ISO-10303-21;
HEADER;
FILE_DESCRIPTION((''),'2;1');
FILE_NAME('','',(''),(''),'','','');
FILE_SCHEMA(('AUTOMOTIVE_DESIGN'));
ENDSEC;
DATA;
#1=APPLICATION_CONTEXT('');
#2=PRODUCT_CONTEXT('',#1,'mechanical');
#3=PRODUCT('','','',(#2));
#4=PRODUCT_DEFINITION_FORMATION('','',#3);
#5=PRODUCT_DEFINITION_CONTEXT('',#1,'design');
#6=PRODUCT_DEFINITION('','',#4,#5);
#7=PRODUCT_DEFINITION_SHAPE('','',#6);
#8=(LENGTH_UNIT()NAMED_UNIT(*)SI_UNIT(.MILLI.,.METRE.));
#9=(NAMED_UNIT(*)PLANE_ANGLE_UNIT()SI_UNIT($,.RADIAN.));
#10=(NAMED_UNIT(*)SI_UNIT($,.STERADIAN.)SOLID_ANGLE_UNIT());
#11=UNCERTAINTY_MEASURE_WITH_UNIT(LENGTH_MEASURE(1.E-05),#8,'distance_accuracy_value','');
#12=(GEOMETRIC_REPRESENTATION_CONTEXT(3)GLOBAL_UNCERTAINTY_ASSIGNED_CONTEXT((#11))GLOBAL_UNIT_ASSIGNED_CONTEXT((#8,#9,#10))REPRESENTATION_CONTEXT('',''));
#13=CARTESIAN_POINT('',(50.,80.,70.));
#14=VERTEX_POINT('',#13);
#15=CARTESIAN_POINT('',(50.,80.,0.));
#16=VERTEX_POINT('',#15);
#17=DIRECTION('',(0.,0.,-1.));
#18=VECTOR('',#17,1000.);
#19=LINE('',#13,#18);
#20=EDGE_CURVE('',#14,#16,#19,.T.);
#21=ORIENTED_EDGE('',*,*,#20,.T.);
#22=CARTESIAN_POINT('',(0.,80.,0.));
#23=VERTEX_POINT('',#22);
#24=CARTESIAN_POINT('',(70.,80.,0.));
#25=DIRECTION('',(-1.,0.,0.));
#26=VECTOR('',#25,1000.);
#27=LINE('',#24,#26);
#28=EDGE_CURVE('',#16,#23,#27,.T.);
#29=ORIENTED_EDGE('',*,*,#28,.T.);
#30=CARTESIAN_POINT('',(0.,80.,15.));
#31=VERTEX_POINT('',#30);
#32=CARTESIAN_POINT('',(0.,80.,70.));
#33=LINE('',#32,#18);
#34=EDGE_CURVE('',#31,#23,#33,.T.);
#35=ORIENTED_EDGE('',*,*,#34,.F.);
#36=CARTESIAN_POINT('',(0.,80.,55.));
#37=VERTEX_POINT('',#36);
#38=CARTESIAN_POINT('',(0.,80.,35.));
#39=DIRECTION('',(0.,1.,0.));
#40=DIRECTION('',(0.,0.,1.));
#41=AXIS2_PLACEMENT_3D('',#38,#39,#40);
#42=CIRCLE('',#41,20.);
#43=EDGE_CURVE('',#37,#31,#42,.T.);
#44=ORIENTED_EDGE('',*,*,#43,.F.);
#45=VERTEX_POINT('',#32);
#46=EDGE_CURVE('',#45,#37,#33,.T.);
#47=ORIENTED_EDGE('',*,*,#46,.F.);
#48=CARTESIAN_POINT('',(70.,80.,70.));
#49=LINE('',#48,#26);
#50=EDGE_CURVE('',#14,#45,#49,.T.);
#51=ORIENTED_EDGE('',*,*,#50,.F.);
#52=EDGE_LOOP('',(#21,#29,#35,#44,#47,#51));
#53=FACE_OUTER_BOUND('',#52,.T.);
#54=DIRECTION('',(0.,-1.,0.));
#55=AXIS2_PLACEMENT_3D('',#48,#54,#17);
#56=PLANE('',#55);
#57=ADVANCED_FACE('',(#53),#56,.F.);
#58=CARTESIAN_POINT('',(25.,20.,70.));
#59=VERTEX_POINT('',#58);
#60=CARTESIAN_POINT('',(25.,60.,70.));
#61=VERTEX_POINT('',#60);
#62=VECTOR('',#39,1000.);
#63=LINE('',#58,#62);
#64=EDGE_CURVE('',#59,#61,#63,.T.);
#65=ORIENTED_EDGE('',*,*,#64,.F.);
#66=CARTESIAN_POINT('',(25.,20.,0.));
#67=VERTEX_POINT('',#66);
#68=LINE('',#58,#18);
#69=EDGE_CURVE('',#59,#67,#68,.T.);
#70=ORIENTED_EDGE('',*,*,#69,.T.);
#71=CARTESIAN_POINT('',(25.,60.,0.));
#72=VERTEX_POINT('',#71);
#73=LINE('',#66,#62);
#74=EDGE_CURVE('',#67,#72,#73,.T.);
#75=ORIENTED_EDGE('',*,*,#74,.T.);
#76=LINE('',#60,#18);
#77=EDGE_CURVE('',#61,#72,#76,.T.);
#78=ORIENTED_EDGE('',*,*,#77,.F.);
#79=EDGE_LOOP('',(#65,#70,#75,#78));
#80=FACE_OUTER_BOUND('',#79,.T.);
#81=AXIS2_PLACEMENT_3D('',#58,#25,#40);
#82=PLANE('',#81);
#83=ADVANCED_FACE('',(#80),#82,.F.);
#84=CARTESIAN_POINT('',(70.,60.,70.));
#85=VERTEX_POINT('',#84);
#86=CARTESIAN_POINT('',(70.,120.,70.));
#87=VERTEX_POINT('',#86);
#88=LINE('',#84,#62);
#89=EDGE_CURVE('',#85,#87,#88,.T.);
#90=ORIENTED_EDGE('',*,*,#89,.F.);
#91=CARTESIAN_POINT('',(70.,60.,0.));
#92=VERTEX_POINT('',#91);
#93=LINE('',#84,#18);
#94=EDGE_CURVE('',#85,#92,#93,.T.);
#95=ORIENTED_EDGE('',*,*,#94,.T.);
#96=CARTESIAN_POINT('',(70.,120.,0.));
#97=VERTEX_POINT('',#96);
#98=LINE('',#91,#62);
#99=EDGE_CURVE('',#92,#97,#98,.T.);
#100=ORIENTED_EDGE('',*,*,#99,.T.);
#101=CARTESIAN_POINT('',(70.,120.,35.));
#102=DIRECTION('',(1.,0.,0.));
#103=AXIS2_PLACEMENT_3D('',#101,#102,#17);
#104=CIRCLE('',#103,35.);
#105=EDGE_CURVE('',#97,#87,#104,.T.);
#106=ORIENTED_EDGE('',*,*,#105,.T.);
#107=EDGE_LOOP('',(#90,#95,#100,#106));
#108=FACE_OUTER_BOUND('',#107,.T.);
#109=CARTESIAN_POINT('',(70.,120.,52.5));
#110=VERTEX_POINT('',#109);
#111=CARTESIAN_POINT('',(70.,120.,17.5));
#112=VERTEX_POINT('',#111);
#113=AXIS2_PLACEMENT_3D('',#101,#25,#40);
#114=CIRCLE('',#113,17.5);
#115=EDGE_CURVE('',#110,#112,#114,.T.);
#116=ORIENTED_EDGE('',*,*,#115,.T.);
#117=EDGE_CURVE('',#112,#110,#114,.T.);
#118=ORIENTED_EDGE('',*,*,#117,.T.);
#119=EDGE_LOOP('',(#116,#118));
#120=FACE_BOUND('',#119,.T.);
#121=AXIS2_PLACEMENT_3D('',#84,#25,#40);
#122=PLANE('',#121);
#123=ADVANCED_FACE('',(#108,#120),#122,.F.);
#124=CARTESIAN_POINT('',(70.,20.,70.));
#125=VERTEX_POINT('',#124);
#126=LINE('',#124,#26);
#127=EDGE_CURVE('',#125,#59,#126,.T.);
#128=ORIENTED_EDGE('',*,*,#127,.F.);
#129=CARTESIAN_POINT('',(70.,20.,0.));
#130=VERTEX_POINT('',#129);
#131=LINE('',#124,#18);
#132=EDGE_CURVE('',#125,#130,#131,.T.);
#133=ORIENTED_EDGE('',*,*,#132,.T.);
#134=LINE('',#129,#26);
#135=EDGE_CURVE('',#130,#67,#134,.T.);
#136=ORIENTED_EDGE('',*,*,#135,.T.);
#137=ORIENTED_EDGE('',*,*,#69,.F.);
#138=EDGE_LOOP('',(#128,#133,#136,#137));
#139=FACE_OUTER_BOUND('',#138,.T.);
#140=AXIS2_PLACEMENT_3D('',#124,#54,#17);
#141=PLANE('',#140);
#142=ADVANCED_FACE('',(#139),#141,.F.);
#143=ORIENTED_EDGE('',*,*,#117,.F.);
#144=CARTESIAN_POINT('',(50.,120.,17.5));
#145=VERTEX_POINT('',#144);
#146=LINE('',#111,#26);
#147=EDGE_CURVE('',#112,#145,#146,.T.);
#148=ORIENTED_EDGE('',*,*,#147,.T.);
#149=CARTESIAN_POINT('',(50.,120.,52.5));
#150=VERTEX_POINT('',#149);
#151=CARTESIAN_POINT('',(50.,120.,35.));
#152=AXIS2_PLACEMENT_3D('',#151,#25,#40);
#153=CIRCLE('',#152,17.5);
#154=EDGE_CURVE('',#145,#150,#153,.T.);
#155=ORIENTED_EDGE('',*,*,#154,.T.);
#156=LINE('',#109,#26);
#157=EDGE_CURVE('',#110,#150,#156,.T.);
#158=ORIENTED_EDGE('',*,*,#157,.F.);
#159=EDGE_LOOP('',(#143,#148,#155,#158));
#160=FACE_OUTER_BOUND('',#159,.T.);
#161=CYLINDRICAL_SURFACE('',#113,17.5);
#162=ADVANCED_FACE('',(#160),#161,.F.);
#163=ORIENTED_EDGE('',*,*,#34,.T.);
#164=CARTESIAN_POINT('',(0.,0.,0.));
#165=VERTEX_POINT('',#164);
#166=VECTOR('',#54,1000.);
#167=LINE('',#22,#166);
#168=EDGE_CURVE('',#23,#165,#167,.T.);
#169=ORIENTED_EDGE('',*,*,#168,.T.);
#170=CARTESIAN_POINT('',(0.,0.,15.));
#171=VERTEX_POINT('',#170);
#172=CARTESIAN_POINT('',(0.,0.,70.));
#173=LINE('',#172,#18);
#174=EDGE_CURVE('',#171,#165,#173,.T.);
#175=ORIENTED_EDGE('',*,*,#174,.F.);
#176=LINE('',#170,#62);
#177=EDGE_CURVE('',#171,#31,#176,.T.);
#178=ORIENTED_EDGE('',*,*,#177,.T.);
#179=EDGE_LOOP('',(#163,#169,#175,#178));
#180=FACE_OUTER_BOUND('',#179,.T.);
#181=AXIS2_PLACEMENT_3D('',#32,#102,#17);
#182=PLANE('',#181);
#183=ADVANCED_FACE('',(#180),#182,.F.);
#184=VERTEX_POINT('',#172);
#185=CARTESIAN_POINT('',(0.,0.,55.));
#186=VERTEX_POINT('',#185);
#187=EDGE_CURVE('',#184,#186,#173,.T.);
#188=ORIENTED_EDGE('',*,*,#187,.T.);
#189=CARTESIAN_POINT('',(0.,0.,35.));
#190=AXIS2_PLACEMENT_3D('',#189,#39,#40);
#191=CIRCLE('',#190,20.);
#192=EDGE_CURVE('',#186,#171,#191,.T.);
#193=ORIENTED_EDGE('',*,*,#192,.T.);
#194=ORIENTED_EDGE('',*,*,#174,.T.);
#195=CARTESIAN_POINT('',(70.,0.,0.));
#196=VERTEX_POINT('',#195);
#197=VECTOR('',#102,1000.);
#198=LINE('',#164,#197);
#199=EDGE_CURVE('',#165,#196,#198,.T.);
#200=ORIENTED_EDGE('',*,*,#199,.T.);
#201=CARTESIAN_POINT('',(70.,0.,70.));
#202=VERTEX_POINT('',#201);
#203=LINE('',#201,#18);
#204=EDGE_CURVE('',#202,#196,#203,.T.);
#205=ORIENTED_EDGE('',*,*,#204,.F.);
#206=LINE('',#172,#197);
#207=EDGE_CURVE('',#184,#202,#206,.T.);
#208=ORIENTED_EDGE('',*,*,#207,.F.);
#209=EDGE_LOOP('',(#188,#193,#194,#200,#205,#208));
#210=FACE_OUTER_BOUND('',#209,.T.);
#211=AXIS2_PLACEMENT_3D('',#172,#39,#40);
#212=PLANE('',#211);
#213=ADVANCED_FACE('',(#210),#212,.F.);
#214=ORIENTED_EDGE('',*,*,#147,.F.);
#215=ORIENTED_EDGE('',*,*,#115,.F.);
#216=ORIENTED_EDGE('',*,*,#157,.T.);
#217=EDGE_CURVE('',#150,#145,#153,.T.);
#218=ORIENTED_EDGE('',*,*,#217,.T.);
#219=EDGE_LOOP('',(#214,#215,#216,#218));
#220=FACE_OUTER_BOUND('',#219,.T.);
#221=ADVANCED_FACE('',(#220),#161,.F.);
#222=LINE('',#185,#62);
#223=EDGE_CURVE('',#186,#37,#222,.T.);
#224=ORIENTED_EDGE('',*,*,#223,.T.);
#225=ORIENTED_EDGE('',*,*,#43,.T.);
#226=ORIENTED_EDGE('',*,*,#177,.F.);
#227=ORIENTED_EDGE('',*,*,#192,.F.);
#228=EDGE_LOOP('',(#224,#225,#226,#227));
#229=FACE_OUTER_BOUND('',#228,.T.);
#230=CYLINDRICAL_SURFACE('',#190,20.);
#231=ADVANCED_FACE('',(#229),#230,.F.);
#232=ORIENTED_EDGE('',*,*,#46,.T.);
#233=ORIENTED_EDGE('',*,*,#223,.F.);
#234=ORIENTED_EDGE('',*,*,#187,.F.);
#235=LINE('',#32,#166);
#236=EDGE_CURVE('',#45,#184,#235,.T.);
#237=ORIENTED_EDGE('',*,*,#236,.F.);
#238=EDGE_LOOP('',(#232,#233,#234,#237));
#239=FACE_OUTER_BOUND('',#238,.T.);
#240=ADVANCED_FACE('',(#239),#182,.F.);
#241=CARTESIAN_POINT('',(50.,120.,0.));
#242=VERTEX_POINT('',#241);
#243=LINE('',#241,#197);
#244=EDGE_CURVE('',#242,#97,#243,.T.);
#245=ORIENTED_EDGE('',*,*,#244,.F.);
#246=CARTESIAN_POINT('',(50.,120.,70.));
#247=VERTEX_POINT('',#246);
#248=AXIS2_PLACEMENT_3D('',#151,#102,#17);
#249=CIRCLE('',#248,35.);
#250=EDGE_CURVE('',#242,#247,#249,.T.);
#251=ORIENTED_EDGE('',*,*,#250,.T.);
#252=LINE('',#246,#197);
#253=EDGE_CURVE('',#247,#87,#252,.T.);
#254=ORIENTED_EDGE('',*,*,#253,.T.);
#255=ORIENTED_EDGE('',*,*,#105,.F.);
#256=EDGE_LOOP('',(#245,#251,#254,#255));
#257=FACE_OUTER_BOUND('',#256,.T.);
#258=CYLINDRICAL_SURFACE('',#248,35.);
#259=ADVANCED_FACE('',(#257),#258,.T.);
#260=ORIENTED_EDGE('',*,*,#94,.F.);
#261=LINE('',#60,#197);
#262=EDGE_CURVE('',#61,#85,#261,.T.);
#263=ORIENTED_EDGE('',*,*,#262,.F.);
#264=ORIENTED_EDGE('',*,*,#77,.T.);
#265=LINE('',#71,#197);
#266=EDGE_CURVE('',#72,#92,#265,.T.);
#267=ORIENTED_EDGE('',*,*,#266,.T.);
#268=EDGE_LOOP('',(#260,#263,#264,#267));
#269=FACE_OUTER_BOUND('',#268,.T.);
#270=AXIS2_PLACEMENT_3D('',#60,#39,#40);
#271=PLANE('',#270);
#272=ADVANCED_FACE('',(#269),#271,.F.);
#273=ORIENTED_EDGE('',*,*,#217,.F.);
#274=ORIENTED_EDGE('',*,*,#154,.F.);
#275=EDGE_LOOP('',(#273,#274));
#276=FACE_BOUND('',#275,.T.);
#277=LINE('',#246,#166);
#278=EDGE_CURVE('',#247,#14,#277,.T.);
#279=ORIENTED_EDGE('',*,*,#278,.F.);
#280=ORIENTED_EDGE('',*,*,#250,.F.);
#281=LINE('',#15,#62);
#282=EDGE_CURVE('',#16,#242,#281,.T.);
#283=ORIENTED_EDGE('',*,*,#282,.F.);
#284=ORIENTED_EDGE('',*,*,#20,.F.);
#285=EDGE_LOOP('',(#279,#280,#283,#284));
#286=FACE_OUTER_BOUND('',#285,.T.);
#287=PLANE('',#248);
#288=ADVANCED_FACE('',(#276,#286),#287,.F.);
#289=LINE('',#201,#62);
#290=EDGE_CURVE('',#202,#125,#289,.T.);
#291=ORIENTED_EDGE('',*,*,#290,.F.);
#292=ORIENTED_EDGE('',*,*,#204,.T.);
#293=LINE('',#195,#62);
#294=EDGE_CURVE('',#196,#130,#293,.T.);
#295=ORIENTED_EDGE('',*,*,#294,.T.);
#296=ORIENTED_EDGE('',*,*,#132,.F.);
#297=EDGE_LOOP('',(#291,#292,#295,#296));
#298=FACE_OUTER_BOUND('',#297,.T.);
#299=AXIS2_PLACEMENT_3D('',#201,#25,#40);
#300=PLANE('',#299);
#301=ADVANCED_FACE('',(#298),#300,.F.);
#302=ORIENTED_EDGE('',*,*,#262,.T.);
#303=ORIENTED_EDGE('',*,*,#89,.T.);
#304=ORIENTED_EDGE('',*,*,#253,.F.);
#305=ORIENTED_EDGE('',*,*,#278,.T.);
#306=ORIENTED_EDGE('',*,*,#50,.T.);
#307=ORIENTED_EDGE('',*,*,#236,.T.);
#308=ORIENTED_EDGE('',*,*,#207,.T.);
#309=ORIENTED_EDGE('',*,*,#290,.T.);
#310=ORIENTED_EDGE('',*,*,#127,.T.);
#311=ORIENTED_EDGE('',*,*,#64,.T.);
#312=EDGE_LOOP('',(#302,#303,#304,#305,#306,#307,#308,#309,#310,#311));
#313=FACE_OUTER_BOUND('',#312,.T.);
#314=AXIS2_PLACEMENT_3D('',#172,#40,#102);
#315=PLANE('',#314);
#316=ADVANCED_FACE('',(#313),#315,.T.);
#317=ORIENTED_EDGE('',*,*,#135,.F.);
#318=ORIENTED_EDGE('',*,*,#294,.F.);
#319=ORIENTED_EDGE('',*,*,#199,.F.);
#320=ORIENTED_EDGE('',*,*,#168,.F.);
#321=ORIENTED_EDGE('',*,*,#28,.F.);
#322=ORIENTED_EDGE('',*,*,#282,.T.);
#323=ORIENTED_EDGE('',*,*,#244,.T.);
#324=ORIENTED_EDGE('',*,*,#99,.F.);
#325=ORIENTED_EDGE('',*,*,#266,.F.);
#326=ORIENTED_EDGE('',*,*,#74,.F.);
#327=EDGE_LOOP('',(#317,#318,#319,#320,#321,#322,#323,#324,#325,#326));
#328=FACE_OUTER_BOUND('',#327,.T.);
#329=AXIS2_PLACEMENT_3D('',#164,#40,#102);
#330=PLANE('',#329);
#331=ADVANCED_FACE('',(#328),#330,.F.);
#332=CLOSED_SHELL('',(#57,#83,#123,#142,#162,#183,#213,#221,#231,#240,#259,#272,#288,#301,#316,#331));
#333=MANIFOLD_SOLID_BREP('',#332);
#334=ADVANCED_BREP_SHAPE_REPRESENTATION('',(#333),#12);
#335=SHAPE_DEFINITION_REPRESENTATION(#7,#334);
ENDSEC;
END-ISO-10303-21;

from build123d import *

# Parameters (mm, degrees)
BRACKET_BODY_DEPTH     = 70
ARC_NOTCH_CUT_DEPTH    = 80
LUG_DEPTH              = 20
LUG_HOLE_SKETCH_R      = 17.5
LUG_THROUGH_HOLE_DEPTH = 20


with BuildPart() as part:
    # Bracket Profile Sketch → Bracket Body (new body)
    with BuildSketch(Plane.XY):
        Polygon((0, 0), (70, 0), (70, 20), (25, 20), (25, 60), (70, 60), (70, 80), (0, 80), align=None)
    extrude(amount=BRACKET_BODY_DEPTH)

    # Arc Notch Sketch → Arc Notch Cut (cut)
    with BuildSketch(Plane(origin=(0, 80, 0), x_dir=(1, 0, 0), z_dir=(0, 1, 0))):
        with BuildLine():
            Line((0, -15), (0, -55))
            ThreePointArc((0, -55), (20, -35), (0, -15))
        make_face()
    extrude(amount=-ARC_NOTCH_CUT_DEPTH, mode=Mode.SUBTRACT)

    # Lug Profile Sketch → Lug (add)
    with BuildSketch(Plane(origin=(70, 0, 0), x_dir=(0, 0, -1), z_dir=(1, 0, 0))):
        with BuildLine():
            Line((-70, 120), (-70, 80))
            Line((-70, 80), (0, 80))
            Line((0, 80), (0, 120))
            ThreePointArc((0, 120), (-35, 155), (-70, 120))
        make_face()
    extrude(amount=-LUG_DEPTH)

    # Lug Hole Sketch → Lug Through Hole (cut)
    with BuildSketch(Plane.ZY.offset(-50)):
        with Locations((35, 120)):
            Circle(LUG_HOLE_SKETCH_R)
    extrude(amount=-LUG_THROUGH_HOLE_DEPTH, mode=Mode.SUBTRACT)


solid = part.part
